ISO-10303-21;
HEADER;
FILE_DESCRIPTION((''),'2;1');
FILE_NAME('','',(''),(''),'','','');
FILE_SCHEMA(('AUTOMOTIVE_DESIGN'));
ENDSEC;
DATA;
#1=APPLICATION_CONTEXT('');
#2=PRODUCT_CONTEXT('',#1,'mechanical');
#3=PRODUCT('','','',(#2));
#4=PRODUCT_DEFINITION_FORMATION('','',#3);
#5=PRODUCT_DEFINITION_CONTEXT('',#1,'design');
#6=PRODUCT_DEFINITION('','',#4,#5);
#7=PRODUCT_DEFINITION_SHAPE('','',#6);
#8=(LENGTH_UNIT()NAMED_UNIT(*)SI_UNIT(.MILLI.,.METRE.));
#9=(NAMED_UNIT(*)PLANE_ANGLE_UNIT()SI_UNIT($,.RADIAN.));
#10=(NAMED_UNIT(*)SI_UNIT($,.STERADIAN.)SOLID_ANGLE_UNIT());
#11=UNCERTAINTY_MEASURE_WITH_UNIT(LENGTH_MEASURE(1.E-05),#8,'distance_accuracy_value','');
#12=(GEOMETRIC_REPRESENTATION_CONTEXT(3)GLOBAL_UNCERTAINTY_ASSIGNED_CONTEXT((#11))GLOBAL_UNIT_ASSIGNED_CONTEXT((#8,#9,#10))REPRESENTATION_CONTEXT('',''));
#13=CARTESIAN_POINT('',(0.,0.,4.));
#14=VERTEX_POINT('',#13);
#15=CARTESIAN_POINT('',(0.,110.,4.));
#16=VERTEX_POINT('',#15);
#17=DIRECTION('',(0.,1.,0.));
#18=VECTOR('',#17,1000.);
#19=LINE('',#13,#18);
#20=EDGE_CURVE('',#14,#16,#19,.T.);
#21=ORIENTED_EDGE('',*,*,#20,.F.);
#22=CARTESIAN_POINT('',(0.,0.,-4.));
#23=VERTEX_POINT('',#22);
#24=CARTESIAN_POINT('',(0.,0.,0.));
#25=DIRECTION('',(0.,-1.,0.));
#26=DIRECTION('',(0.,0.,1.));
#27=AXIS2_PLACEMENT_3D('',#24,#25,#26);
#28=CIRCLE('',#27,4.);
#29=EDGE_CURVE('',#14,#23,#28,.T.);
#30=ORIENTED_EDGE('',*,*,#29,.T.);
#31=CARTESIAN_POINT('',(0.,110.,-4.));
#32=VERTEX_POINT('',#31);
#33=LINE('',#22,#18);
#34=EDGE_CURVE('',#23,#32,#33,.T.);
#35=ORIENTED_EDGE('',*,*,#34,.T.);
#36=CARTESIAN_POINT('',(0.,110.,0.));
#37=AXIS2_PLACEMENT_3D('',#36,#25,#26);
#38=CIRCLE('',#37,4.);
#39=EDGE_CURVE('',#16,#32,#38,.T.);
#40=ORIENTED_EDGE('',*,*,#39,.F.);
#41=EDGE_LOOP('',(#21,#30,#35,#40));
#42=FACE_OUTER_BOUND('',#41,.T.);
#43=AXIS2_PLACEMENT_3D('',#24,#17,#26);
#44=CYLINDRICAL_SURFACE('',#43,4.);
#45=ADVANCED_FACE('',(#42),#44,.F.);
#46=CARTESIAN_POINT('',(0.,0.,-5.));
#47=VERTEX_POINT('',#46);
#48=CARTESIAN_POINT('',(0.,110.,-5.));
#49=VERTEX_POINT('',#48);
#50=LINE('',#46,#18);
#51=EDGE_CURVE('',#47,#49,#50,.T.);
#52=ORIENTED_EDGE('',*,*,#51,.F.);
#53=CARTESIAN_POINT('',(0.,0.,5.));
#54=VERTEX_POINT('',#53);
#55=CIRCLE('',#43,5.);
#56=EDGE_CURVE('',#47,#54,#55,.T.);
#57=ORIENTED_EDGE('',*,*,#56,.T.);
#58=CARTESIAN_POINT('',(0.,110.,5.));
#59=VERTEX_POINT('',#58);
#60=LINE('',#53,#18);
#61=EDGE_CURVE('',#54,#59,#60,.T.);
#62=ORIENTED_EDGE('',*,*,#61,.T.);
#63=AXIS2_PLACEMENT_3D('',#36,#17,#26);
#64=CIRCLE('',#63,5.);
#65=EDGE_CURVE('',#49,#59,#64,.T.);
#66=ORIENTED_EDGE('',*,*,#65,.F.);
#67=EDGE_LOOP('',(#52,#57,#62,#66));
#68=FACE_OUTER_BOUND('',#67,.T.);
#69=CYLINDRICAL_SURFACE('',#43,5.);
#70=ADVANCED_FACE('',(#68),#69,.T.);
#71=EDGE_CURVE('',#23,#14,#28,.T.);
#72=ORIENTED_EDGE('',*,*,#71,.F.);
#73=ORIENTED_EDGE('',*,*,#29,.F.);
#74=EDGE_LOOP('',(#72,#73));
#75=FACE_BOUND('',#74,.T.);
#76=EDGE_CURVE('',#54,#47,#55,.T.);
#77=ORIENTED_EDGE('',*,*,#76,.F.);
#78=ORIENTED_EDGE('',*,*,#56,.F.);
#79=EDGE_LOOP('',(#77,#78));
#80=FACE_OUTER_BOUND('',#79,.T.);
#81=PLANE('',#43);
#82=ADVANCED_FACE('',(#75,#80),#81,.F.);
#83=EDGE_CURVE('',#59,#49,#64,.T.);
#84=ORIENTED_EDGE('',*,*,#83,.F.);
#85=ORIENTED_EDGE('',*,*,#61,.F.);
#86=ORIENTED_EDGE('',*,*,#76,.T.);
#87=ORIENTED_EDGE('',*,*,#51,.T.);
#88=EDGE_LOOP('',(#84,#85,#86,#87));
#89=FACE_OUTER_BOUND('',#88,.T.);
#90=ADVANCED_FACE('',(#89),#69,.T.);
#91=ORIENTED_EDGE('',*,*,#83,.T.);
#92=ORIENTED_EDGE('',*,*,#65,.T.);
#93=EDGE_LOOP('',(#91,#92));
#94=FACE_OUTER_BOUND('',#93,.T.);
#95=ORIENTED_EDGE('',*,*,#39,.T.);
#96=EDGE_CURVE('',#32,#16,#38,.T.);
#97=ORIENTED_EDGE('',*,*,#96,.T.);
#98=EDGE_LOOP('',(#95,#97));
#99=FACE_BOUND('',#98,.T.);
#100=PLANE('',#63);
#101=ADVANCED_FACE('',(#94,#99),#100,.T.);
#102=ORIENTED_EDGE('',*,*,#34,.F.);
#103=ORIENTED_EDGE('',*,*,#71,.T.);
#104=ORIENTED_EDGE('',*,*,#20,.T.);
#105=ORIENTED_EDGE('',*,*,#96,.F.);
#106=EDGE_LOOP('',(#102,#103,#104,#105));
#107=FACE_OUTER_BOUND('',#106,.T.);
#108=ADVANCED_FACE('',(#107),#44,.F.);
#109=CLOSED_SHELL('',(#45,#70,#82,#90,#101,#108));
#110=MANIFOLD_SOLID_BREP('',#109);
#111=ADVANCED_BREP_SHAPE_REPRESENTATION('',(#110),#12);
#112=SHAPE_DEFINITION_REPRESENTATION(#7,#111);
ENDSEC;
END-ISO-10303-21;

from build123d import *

# Parameters (mm, degrees)
SKETCH_2_R   = 5
SKETCH_2_R_2 = 4


with BuildPart() as part:
    # 扫描1: sweep along a path in 草图1
    with BuildLine(Plane.XY) as sweep_1_path:
        Line((0, 0), (0, 110))
    # 草图2 → 扫描1 (sweep)
    with BuildSketch(Plane(origin=(0, 0, 0), x_dir=(1, 0, 0), z_dir=(0, 1, 0))):
        Circle(SKETCH_2_R)
        Circle(SKETCH_2_R_2, mode=Mode.SUBTRACT)
    sweep(path=sweep_1_path.line)


solid = part.part
